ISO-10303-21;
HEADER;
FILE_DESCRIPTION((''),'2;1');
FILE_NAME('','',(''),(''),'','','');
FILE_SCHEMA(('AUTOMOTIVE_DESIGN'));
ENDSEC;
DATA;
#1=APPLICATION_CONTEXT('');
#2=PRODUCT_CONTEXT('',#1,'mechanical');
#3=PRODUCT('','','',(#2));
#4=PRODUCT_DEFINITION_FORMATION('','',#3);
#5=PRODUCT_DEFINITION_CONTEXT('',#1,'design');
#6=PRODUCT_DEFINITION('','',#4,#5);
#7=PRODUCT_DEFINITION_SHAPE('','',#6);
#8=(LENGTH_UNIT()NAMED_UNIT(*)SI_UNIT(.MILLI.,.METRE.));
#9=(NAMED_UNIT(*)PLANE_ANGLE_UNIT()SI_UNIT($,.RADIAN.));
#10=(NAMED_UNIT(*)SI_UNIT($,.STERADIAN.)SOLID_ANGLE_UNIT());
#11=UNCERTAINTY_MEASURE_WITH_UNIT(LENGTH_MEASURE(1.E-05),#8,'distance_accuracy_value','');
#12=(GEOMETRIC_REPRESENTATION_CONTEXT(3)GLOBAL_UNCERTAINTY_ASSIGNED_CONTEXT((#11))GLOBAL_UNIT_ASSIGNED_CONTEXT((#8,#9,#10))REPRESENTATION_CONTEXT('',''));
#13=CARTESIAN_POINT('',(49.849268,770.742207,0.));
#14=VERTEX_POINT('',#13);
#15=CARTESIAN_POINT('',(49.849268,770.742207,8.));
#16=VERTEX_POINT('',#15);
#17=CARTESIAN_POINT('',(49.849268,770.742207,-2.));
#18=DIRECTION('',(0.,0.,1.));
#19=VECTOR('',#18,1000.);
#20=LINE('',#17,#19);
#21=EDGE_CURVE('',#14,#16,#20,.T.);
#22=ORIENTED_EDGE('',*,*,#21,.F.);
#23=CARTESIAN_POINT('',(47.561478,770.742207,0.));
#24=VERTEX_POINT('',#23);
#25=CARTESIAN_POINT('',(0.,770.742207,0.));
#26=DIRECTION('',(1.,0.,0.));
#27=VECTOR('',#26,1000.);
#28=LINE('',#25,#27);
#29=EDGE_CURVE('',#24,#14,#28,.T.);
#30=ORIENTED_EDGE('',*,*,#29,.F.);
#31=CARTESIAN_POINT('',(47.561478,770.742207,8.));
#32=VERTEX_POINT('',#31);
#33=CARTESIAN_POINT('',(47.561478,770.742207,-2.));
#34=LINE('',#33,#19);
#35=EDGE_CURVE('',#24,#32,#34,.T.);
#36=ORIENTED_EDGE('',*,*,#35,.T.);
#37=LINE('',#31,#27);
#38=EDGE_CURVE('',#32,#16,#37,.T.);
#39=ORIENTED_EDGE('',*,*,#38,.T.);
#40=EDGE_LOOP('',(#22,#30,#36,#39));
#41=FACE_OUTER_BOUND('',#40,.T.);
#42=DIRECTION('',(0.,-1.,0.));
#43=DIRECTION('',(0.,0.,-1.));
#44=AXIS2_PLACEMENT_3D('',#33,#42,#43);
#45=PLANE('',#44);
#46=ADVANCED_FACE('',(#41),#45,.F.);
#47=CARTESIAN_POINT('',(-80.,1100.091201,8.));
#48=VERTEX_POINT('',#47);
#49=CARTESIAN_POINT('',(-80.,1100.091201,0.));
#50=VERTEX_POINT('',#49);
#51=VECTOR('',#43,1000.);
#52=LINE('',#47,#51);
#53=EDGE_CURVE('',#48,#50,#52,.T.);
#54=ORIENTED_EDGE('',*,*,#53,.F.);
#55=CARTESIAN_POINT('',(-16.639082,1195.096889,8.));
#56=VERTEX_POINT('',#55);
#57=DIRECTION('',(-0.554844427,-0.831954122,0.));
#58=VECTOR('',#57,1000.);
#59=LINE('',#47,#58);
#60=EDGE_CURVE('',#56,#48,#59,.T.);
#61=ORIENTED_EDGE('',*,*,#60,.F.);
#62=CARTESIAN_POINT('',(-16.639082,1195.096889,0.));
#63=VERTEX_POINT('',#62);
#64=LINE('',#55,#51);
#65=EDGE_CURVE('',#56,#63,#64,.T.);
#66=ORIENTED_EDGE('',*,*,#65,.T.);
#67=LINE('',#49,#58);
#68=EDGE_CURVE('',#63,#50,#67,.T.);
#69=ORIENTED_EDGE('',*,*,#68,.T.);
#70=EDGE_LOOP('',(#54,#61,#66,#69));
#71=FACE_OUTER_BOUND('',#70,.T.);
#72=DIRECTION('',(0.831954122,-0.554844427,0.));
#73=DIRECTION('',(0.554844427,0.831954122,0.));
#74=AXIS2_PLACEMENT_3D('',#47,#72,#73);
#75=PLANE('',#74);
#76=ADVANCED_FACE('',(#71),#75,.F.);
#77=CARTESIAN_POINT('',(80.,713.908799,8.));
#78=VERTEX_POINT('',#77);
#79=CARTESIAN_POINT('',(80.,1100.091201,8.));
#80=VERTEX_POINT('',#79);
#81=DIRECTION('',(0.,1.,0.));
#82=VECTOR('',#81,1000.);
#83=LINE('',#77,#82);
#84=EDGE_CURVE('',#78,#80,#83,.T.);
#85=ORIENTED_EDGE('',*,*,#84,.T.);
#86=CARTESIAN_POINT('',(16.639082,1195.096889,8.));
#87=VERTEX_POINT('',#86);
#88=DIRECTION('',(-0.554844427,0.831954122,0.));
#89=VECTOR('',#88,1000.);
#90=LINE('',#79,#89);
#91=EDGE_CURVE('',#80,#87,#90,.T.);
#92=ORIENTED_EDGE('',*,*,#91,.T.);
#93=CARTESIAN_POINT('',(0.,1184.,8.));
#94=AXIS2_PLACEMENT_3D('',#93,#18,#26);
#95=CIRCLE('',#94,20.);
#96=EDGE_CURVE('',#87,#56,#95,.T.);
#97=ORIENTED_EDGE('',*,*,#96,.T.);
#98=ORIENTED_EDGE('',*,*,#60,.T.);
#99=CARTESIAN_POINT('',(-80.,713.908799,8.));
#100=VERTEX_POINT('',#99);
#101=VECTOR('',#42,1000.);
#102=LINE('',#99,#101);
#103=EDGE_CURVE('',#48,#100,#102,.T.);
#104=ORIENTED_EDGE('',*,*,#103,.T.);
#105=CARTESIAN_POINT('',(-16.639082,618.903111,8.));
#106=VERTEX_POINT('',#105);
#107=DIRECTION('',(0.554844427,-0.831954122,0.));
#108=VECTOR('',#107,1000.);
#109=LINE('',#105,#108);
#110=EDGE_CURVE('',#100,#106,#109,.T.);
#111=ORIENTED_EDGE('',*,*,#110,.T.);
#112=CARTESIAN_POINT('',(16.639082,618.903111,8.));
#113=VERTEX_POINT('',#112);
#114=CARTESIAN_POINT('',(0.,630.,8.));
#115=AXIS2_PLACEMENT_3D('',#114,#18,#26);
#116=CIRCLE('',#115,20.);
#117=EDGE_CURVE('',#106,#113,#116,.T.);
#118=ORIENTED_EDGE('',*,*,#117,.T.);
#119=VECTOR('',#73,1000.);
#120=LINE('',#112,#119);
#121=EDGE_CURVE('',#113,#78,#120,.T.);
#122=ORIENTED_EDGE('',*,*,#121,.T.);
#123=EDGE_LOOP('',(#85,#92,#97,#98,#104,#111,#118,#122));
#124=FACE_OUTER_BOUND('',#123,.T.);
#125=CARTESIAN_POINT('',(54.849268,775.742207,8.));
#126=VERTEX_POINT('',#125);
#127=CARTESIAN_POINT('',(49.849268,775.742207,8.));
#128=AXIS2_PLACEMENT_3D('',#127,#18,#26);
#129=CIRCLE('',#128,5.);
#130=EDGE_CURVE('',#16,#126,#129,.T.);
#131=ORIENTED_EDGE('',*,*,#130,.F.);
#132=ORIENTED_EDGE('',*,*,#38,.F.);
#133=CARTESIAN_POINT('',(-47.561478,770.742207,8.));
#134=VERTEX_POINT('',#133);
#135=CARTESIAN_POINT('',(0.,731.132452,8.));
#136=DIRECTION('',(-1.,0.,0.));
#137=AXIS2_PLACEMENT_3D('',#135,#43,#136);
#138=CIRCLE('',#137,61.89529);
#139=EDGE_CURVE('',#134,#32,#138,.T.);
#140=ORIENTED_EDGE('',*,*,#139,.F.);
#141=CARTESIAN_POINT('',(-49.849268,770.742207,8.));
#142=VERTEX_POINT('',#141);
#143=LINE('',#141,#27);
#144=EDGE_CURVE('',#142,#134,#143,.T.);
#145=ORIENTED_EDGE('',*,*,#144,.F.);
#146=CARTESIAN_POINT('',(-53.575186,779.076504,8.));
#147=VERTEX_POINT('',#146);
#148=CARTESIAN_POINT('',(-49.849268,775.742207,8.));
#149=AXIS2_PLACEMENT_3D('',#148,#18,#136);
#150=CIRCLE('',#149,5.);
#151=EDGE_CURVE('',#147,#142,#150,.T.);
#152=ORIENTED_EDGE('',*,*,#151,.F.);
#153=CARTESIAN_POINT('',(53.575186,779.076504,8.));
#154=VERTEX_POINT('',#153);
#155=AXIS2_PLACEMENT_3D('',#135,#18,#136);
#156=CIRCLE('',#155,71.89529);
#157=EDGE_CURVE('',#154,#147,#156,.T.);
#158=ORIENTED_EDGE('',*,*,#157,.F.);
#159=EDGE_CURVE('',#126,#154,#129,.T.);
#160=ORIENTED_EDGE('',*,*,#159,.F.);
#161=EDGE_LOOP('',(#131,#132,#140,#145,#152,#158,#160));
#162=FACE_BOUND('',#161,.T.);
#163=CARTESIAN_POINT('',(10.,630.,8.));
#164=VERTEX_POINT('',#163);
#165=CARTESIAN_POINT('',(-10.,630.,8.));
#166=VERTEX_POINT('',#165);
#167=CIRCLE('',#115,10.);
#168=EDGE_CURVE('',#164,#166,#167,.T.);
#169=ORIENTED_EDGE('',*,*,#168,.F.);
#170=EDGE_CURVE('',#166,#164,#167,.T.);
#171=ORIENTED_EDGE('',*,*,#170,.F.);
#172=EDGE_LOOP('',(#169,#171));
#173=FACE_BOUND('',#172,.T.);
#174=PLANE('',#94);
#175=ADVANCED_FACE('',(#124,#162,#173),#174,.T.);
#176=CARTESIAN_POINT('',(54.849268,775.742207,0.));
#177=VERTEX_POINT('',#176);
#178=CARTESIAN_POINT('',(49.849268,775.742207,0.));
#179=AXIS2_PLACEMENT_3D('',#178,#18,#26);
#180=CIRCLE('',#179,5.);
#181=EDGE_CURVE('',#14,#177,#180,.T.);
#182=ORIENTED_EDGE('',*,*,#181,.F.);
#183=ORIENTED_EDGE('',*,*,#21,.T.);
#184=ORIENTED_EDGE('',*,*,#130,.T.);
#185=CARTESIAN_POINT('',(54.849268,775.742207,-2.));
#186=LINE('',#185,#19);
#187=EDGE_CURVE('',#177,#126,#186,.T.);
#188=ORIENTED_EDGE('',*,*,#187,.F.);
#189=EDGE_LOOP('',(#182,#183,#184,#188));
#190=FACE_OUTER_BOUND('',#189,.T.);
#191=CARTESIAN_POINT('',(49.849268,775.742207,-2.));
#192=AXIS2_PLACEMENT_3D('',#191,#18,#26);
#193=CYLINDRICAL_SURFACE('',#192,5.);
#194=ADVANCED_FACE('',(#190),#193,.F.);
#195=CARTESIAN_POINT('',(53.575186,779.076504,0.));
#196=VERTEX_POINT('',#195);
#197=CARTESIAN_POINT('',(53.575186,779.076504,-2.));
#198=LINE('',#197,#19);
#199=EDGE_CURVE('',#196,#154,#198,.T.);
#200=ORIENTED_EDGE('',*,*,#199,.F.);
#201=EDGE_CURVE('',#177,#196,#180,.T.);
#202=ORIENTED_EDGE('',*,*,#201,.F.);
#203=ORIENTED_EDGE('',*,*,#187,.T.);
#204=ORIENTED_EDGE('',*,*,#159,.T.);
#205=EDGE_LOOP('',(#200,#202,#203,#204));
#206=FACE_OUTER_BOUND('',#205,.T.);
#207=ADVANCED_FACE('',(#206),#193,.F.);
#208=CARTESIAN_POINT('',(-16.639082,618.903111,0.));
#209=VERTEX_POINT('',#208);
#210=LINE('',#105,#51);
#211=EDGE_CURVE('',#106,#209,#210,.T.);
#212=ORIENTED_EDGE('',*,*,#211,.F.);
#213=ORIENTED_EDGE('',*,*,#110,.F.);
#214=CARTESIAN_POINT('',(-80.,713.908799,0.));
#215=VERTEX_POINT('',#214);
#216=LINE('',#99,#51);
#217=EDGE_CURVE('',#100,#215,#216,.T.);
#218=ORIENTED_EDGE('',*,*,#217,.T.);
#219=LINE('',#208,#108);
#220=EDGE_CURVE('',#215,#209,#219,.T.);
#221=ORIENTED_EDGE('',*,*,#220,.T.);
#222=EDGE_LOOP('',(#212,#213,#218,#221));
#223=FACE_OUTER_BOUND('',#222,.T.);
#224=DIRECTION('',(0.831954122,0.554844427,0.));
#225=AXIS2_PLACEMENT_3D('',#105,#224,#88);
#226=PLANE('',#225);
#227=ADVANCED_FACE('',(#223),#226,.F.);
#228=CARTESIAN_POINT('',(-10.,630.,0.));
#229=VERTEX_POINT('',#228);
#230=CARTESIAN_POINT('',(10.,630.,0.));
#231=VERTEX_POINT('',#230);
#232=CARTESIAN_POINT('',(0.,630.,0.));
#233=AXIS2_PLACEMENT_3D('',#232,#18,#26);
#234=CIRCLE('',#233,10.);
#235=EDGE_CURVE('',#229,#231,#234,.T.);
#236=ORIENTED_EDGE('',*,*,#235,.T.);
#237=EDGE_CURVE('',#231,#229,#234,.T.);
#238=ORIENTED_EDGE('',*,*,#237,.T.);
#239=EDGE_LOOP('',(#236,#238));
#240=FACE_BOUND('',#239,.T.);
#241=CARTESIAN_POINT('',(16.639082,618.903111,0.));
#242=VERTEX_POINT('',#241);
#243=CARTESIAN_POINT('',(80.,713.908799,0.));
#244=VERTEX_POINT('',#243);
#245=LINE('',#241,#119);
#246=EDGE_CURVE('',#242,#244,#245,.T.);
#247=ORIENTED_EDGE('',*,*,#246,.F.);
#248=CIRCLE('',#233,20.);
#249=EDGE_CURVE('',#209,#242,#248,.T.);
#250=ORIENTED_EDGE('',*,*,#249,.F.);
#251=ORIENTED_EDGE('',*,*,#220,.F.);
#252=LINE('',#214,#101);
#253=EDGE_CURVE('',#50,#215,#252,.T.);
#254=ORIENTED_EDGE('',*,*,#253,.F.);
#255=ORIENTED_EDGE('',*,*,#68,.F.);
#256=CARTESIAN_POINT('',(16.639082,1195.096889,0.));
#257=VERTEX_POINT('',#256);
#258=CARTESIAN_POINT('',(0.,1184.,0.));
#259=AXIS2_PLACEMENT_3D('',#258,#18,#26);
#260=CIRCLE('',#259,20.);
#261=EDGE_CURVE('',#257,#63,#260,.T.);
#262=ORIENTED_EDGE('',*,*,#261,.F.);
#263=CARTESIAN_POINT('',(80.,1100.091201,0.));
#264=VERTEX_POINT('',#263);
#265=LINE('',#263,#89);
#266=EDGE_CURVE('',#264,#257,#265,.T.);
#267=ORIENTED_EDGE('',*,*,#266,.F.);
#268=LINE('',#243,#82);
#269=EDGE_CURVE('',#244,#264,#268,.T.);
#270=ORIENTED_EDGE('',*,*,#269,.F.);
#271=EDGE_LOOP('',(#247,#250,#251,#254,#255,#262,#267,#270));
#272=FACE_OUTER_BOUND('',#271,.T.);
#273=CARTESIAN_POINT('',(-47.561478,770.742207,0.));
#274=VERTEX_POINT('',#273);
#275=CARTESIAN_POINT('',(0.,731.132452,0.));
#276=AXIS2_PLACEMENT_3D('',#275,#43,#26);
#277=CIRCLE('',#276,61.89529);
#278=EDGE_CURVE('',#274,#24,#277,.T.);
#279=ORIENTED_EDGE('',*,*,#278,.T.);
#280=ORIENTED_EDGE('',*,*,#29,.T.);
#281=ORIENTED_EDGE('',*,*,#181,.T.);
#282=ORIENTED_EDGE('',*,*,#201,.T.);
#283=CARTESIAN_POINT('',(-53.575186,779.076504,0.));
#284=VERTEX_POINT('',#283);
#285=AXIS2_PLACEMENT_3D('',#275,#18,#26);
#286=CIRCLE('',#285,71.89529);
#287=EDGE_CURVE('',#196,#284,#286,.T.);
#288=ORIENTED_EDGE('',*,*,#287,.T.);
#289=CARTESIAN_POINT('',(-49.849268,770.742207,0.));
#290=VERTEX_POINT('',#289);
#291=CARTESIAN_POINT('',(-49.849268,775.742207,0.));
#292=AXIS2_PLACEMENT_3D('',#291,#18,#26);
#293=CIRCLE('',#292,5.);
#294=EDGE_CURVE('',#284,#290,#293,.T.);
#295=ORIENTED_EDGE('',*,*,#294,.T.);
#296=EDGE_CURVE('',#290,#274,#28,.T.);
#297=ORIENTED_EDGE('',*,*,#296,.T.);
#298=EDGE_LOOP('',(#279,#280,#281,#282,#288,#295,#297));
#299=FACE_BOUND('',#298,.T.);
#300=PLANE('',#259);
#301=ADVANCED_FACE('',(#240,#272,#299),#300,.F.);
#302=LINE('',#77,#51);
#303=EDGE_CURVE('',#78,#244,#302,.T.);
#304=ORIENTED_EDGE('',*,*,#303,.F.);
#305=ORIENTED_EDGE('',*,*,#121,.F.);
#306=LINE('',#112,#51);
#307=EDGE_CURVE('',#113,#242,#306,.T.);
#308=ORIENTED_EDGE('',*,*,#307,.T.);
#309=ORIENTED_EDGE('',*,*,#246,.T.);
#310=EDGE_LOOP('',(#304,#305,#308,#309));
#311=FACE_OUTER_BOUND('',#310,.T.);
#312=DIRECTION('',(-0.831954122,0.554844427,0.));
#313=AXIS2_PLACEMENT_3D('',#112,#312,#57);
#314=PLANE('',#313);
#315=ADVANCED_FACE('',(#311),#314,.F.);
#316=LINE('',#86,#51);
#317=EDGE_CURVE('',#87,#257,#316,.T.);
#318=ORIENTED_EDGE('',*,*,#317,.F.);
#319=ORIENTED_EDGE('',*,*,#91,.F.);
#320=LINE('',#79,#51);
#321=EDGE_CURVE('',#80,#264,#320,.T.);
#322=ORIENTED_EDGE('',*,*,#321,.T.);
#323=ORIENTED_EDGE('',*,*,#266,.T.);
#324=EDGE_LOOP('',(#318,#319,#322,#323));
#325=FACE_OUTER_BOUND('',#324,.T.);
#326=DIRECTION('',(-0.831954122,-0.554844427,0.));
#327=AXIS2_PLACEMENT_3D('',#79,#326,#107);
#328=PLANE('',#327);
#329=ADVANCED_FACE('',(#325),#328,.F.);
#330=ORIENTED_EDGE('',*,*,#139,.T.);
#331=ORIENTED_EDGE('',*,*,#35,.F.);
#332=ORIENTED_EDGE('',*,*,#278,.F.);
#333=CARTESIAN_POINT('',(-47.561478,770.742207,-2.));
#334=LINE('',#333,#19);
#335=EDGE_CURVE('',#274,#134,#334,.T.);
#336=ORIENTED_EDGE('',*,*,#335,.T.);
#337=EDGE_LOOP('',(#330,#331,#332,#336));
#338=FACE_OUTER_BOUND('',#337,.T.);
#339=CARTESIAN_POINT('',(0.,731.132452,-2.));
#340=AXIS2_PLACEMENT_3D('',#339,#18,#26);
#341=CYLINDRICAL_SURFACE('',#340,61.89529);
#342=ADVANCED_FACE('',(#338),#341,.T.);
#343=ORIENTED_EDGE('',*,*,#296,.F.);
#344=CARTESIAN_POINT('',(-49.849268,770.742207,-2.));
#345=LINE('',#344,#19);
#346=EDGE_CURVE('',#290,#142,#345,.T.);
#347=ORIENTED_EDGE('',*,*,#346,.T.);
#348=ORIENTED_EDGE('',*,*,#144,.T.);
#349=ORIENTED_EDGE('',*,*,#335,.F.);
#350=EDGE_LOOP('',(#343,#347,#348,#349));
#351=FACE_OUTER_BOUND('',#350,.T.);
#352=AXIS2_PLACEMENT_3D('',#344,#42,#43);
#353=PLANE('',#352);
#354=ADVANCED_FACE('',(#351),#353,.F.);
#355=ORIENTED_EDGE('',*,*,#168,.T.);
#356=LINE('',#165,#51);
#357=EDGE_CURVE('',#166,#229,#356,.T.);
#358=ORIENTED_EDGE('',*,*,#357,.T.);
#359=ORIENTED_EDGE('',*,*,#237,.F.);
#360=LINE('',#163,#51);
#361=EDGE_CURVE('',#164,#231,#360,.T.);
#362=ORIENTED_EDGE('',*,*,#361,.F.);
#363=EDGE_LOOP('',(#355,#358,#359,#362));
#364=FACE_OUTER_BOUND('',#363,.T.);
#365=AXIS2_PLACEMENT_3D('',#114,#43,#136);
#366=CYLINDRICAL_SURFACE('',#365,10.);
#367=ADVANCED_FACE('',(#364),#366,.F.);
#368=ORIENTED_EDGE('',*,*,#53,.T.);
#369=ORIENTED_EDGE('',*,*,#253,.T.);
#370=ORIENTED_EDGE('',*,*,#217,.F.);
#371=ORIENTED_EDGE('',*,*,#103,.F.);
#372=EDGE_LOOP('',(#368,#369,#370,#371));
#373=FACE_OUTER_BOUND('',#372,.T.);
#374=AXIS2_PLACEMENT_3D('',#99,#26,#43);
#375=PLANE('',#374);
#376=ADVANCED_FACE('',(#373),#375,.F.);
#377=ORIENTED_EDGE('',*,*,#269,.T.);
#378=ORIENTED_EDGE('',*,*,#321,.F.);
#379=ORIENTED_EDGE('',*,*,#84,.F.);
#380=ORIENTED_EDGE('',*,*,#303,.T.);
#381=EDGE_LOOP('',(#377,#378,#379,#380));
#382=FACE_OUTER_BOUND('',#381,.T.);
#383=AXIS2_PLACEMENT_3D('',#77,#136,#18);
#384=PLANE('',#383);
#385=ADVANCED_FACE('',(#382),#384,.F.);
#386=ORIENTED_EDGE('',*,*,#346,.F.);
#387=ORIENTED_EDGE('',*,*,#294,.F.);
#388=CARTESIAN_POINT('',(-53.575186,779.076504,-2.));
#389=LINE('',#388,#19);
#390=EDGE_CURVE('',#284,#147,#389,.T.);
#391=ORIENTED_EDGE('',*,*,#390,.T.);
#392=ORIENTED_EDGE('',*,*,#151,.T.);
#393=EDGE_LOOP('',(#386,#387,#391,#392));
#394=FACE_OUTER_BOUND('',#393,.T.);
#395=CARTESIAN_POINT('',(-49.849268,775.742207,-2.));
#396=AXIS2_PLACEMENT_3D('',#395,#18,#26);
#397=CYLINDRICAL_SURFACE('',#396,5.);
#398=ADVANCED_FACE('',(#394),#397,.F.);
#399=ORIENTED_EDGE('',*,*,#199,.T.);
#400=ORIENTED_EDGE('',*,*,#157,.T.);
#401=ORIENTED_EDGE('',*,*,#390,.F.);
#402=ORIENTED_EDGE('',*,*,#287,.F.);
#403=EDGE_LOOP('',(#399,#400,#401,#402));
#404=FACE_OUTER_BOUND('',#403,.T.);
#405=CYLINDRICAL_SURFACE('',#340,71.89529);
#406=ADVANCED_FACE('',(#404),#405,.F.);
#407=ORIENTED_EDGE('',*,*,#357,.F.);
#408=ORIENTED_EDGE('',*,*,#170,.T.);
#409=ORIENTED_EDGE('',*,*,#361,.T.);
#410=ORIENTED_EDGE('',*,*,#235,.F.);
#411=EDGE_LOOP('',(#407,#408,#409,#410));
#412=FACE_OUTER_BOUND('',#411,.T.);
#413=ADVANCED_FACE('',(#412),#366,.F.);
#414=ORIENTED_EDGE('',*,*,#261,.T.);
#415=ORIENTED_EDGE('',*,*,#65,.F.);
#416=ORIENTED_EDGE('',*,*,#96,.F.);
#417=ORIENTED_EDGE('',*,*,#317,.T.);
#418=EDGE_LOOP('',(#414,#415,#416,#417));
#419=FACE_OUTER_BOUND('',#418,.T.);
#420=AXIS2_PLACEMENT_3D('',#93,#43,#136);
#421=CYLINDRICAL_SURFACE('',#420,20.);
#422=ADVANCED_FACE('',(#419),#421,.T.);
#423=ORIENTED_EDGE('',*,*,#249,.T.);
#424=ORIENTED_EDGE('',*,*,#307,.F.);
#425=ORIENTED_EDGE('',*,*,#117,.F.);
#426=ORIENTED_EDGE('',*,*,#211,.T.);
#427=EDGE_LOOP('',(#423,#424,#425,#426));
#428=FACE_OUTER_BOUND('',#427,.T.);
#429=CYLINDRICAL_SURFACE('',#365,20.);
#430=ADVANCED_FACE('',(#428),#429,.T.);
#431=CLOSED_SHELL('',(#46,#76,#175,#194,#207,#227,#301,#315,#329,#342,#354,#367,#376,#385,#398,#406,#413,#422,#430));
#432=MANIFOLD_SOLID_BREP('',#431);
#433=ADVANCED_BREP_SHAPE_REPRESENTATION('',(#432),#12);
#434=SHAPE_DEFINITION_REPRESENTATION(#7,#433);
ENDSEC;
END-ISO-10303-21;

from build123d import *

# Parameters (mm, degrees)
SKETCH2_R           = 10
BOSS_EXTRUDE1_DEPTH = 8
CUT_EXTRUDE1_DEPTH  = 10


with BuildPart() as part:
    # Sketch2 → Boss-Extrude1 (new body)
    with BuildSketch(Plane.XY):
        with BuildLine():
            Line((-16.639082443, 618.903111451), (-80, 713.908799417))
            Line((-80, 713.908799417), (-80, 1100.091200583))
            Line((-80, 1100.091200583), (-16.639082443, 1195.096888549))
            ThreePointArc((-16.639082443, 1195.096888549), (0, 1204), (16.639082443, 1195.096888549))
            Line((16.639082443, 1195.096888549), (80, 1100.091200583))
            Line((80, 1100.091200583), (80, 713.908799417))
            Line((80, 713.908799417), (16.639082443, 618.903111451))
            ThreePointArc((16.639082443, 618.903111451), (0, 610), (-16.639082443, 618.903111451))
        make_face()
        with Locations((0, 630)):
            Circle(SKETCH2_R, mode=Mode.SUBTRACT)
    extrude(amount=BOSS_EXTRUDE1_DEPTH)

    # Sketch4 → Cut-Extrude1 (cut)
    with BuildSketch(Plane.XY.offset(8)):
        with BuildLine():
            Line((-49.84926833, 770.742207295), (-47.561478164, 770.742207295))
            ThreePointArc((-47.561478164, 770.742207295), (0, 793.027742088), (47.561478164, 770.742207295))
            Line((47.561478164, 770.742207295), (49.84926833, 770.742207295))
            ThreePointArc((49.84926833, 770.742207295), (54.413886924, 773.70155615), (53.575185994, 779.076504457))
            ThreePointArc((53.575185994, 779.076504457), (0, 803.027742088), (-53.575185994, 779.076504457))
            ThreePointArc((-53.575185994, 779.076504457), (-54.413886924, 773.70155615), (-49.84926833, 770.742207295))
        make_face()
    extrude(amount=-CUT_EXTRUDE1_DEPTH, mode=Mode.SUBTRACT)


solid = part.part
